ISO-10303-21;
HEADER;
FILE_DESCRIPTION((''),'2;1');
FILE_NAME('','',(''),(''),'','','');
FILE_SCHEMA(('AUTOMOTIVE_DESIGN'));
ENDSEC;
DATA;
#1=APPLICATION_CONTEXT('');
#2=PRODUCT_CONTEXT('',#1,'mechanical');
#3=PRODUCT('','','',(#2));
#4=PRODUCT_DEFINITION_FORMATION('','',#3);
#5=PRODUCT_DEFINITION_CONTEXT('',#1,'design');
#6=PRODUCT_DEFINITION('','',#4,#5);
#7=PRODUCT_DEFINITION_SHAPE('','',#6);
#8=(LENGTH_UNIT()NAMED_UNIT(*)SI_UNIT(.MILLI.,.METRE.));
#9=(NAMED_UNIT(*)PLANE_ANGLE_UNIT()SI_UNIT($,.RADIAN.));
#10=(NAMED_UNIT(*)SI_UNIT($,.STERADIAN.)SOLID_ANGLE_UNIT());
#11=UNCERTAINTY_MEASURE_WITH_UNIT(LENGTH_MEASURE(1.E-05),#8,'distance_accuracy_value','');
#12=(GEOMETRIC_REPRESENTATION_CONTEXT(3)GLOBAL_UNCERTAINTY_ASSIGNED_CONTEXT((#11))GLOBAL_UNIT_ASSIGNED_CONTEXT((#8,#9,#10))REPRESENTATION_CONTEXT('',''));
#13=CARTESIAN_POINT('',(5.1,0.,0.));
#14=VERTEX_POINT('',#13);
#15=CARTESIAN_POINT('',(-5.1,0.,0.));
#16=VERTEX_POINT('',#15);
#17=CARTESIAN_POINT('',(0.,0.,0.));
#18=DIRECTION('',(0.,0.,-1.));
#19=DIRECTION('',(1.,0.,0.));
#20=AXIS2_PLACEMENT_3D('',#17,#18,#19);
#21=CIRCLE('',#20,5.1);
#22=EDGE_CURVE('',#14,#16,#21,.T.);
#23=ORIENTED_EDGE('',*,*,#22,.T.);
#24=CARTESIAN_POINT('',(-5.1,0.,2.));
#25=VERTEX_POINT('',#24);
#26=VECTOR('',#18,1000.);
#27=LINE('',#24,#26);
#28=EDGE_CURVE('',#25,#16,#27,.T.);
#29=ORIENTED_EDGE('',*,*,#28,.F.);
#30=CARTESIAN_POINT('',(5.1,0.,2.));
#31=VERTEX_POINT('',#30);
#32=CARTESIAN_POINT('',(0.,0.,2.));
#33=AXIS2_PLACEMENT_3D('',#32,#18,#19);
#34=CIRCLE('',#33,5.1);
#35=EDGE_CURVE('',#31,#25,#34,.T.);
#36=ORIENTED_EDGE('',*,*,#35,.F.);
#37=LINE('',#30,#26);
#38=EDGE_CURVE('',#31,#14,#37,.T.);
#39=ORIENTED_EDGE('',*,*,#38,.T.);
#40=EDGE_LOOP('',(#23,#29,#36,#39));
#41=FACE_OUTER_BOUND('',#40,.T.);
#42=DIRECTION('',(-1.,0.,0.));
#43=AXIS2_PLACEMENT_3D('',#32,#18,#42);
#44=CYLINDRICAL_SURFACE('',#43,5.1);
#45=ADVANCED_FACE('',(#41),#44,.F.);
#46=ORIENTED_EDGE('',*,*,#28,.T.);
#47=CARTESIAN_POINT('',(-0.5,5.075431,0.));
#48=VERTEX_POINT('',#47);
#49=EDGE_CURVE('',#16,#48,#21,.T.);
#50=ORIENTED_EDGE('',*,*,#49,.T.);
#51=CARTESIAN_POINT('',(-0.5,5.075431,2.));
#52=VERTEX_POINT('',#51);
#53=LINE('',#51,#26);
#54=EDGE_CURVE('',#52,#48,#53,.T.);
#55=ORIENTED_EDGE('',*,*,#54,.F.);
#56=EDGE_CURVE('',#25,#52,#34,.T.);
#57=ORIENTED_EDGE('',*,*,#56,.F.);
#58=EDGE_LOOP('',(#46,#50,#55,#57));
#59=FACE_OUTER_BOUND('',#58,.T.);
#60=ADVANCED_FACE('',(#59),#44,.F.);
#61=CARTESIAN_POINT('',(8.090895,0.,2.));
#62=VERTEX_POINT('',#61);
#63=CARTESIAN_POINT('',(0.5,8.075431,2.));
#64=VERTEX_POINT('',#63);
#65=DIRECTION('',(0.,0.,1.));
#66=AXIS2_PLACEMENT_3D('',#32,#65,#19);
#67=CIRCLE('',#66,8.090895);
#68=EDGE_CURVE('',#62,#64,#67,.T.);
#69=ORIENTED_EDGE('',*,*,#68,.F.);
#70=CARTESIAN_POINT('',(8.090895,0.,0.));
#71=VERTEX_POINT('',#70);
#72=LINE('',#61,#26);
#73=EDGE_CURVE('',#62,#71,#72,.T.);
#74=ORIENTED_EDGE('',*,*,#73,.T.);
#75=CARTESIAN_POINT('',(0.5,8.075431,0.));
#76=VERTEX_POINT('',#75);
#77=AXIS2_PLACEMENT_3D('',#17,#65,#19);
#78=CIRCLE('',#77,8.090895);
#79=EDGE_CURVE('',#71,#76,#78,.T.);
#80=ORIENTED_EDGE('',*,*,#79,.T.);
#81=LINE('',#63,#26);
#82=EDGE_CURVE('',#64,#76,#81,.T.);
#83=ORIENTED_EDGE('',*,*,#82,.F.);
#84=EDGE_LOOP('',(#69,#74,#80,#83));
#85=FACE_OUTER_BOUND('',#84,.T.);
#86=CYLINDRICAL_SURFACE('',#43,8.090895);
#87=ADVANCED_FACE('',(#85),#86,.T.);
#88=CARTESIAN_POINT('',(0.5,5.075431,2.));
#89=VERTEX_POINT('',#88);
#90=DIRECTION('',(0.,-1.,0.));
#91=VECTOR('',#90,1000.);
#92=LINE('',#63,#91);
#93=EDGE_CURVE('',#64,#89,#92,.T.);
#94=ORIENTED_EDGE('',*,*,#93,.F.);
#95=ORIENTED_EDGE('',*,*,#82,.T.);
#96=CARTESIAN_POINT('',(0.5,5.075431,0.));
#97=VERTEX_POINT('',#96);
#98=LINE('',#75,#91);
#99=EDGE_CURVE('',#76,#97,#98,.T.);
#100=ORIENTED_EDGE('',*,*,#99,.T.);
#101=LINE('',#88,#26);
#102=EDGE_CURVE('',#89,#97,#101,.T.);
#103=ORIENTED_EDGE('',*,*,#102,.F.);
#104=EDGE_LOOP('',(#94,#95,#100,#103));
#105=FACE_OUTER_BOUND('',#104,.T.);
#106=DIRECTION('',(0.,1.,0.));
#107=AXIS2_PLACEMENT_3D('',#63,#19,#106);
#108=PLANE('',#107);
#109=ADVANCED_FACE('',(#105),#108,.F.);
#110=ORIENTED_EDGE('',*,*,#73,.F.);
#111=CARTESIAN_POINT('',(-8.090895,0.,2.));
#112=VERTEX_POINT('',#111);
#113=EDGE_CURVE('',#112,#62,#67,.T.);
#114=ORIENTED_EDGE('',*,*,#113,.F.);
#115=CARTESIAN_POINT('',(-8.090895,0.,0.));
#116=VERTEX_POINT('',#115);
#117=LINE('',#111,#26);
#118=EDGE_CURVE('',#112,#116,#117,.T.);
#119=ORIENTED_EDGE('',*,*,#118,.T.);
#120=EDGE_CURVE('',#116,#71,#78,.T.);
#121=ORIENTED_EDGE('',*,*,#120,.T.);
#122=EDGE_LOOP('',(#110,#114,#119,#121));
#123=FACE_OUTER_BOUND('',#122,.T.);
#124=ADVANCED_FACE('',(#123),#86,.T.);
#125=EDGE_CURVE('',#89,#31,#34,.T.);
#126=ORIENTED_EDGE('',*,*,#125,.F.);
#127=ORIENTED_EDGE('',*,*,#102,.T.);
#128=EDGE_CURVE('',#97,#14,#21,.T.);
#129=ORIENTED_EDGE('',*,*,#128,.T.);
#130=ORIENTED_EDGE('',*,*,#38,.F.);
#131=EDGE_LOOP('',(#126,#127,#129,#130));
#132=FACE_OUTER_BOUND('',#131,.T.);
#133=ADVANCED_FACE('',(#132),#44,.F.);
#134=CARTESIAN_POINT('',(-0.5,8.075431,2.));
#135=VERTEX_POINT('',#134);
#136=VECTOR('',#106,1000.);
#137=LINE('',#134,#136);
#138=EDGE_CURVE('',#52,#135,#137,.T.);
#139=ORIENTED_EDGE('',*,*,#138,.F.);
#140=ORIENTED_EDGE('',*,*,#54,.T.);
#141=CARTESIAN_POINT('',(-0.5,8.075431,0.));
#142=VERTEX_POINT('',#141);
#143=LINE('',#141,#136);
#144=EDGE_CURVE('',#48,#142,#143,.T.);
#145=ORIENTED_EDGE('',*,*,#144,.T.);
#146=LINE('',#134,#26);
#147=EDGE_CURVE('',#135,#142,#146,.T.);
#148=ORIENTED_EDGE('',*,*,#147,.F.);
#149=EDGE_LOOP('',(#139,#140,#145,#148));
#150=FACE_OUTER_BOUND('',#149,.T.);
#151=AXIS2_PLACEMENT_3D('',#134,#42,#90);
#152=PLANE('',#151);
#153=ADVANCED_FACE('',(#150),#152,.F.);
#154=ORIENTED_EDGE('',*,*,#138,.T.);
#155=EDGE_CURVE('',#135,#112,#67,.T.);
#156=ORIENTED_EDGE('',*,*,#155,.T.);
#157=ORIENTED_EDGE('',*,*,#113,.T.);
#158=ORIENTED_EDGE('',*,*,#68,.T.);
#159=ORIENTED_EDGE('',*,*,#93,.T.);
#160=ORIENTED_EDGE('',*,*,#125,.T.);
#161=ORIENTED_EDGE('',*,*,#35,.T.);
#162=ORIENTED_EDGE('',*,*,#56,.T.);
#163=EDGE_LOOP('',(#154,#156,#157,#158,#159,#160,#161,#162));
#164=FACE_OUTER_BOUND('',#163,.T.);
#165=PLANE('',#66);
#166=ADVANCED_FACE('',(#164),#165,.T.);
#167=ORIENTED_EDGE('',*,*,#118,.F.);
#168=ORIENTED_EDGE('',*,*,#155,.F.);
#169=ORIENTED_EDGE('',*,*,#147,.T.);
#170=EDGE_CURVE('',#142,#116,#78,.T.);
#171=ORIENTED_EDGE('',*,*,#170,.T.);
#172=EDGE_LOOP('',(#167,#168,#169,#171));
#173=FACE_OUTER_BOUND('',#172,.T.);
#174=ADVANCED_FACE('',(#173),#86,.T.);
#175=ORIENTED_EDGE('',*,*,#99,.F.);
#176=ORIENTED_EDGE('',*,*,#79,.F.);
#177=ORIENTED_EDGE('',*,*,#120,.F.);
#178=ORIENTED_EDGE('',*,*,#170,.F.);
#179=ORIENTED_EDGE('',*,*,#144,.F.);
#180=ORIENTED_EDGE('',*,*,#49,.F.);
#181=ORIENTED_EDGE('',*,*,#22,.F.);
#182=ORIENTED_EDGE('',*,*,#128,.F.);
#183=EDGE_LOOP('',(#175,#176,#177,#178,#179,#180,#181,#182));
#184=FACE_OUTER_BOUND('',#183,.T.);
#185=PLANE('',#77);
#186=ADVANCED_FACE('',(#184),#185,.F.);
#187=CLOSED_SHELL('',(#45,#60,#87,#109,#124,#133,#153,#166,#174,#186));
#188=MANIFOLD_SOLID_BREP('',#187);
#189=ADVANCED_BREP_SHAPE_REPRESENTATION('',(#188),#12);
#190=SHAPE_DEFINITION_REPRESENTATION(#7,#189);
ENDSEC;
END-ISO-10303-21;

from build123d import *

# Parameters (mm, degrees)
EXTRUDE_1_DEPTH = 2


with BuildPart() as part:
    # Sketch 263 → 拉伸1 (new body)
    with BuildSketch(Plane.XY):
        with BuildLine():
            Line((-0.5, 8.075431016), (-0.5, 5.075431016))
            ThreePointArc((-0.5, 5.075431016), (0, -5.1), (0.5, 5.075431016))
            Line((0.5, 5.075431016), (0.5, 8.075431016))
            ThreePointArc((0.5, 8.075431016), (0, -8.090895259), (-0.5, 8.075431016))
        make_face()
    extrude(amount=EXTRUDE_1_DEPTH)


solid = part.part
